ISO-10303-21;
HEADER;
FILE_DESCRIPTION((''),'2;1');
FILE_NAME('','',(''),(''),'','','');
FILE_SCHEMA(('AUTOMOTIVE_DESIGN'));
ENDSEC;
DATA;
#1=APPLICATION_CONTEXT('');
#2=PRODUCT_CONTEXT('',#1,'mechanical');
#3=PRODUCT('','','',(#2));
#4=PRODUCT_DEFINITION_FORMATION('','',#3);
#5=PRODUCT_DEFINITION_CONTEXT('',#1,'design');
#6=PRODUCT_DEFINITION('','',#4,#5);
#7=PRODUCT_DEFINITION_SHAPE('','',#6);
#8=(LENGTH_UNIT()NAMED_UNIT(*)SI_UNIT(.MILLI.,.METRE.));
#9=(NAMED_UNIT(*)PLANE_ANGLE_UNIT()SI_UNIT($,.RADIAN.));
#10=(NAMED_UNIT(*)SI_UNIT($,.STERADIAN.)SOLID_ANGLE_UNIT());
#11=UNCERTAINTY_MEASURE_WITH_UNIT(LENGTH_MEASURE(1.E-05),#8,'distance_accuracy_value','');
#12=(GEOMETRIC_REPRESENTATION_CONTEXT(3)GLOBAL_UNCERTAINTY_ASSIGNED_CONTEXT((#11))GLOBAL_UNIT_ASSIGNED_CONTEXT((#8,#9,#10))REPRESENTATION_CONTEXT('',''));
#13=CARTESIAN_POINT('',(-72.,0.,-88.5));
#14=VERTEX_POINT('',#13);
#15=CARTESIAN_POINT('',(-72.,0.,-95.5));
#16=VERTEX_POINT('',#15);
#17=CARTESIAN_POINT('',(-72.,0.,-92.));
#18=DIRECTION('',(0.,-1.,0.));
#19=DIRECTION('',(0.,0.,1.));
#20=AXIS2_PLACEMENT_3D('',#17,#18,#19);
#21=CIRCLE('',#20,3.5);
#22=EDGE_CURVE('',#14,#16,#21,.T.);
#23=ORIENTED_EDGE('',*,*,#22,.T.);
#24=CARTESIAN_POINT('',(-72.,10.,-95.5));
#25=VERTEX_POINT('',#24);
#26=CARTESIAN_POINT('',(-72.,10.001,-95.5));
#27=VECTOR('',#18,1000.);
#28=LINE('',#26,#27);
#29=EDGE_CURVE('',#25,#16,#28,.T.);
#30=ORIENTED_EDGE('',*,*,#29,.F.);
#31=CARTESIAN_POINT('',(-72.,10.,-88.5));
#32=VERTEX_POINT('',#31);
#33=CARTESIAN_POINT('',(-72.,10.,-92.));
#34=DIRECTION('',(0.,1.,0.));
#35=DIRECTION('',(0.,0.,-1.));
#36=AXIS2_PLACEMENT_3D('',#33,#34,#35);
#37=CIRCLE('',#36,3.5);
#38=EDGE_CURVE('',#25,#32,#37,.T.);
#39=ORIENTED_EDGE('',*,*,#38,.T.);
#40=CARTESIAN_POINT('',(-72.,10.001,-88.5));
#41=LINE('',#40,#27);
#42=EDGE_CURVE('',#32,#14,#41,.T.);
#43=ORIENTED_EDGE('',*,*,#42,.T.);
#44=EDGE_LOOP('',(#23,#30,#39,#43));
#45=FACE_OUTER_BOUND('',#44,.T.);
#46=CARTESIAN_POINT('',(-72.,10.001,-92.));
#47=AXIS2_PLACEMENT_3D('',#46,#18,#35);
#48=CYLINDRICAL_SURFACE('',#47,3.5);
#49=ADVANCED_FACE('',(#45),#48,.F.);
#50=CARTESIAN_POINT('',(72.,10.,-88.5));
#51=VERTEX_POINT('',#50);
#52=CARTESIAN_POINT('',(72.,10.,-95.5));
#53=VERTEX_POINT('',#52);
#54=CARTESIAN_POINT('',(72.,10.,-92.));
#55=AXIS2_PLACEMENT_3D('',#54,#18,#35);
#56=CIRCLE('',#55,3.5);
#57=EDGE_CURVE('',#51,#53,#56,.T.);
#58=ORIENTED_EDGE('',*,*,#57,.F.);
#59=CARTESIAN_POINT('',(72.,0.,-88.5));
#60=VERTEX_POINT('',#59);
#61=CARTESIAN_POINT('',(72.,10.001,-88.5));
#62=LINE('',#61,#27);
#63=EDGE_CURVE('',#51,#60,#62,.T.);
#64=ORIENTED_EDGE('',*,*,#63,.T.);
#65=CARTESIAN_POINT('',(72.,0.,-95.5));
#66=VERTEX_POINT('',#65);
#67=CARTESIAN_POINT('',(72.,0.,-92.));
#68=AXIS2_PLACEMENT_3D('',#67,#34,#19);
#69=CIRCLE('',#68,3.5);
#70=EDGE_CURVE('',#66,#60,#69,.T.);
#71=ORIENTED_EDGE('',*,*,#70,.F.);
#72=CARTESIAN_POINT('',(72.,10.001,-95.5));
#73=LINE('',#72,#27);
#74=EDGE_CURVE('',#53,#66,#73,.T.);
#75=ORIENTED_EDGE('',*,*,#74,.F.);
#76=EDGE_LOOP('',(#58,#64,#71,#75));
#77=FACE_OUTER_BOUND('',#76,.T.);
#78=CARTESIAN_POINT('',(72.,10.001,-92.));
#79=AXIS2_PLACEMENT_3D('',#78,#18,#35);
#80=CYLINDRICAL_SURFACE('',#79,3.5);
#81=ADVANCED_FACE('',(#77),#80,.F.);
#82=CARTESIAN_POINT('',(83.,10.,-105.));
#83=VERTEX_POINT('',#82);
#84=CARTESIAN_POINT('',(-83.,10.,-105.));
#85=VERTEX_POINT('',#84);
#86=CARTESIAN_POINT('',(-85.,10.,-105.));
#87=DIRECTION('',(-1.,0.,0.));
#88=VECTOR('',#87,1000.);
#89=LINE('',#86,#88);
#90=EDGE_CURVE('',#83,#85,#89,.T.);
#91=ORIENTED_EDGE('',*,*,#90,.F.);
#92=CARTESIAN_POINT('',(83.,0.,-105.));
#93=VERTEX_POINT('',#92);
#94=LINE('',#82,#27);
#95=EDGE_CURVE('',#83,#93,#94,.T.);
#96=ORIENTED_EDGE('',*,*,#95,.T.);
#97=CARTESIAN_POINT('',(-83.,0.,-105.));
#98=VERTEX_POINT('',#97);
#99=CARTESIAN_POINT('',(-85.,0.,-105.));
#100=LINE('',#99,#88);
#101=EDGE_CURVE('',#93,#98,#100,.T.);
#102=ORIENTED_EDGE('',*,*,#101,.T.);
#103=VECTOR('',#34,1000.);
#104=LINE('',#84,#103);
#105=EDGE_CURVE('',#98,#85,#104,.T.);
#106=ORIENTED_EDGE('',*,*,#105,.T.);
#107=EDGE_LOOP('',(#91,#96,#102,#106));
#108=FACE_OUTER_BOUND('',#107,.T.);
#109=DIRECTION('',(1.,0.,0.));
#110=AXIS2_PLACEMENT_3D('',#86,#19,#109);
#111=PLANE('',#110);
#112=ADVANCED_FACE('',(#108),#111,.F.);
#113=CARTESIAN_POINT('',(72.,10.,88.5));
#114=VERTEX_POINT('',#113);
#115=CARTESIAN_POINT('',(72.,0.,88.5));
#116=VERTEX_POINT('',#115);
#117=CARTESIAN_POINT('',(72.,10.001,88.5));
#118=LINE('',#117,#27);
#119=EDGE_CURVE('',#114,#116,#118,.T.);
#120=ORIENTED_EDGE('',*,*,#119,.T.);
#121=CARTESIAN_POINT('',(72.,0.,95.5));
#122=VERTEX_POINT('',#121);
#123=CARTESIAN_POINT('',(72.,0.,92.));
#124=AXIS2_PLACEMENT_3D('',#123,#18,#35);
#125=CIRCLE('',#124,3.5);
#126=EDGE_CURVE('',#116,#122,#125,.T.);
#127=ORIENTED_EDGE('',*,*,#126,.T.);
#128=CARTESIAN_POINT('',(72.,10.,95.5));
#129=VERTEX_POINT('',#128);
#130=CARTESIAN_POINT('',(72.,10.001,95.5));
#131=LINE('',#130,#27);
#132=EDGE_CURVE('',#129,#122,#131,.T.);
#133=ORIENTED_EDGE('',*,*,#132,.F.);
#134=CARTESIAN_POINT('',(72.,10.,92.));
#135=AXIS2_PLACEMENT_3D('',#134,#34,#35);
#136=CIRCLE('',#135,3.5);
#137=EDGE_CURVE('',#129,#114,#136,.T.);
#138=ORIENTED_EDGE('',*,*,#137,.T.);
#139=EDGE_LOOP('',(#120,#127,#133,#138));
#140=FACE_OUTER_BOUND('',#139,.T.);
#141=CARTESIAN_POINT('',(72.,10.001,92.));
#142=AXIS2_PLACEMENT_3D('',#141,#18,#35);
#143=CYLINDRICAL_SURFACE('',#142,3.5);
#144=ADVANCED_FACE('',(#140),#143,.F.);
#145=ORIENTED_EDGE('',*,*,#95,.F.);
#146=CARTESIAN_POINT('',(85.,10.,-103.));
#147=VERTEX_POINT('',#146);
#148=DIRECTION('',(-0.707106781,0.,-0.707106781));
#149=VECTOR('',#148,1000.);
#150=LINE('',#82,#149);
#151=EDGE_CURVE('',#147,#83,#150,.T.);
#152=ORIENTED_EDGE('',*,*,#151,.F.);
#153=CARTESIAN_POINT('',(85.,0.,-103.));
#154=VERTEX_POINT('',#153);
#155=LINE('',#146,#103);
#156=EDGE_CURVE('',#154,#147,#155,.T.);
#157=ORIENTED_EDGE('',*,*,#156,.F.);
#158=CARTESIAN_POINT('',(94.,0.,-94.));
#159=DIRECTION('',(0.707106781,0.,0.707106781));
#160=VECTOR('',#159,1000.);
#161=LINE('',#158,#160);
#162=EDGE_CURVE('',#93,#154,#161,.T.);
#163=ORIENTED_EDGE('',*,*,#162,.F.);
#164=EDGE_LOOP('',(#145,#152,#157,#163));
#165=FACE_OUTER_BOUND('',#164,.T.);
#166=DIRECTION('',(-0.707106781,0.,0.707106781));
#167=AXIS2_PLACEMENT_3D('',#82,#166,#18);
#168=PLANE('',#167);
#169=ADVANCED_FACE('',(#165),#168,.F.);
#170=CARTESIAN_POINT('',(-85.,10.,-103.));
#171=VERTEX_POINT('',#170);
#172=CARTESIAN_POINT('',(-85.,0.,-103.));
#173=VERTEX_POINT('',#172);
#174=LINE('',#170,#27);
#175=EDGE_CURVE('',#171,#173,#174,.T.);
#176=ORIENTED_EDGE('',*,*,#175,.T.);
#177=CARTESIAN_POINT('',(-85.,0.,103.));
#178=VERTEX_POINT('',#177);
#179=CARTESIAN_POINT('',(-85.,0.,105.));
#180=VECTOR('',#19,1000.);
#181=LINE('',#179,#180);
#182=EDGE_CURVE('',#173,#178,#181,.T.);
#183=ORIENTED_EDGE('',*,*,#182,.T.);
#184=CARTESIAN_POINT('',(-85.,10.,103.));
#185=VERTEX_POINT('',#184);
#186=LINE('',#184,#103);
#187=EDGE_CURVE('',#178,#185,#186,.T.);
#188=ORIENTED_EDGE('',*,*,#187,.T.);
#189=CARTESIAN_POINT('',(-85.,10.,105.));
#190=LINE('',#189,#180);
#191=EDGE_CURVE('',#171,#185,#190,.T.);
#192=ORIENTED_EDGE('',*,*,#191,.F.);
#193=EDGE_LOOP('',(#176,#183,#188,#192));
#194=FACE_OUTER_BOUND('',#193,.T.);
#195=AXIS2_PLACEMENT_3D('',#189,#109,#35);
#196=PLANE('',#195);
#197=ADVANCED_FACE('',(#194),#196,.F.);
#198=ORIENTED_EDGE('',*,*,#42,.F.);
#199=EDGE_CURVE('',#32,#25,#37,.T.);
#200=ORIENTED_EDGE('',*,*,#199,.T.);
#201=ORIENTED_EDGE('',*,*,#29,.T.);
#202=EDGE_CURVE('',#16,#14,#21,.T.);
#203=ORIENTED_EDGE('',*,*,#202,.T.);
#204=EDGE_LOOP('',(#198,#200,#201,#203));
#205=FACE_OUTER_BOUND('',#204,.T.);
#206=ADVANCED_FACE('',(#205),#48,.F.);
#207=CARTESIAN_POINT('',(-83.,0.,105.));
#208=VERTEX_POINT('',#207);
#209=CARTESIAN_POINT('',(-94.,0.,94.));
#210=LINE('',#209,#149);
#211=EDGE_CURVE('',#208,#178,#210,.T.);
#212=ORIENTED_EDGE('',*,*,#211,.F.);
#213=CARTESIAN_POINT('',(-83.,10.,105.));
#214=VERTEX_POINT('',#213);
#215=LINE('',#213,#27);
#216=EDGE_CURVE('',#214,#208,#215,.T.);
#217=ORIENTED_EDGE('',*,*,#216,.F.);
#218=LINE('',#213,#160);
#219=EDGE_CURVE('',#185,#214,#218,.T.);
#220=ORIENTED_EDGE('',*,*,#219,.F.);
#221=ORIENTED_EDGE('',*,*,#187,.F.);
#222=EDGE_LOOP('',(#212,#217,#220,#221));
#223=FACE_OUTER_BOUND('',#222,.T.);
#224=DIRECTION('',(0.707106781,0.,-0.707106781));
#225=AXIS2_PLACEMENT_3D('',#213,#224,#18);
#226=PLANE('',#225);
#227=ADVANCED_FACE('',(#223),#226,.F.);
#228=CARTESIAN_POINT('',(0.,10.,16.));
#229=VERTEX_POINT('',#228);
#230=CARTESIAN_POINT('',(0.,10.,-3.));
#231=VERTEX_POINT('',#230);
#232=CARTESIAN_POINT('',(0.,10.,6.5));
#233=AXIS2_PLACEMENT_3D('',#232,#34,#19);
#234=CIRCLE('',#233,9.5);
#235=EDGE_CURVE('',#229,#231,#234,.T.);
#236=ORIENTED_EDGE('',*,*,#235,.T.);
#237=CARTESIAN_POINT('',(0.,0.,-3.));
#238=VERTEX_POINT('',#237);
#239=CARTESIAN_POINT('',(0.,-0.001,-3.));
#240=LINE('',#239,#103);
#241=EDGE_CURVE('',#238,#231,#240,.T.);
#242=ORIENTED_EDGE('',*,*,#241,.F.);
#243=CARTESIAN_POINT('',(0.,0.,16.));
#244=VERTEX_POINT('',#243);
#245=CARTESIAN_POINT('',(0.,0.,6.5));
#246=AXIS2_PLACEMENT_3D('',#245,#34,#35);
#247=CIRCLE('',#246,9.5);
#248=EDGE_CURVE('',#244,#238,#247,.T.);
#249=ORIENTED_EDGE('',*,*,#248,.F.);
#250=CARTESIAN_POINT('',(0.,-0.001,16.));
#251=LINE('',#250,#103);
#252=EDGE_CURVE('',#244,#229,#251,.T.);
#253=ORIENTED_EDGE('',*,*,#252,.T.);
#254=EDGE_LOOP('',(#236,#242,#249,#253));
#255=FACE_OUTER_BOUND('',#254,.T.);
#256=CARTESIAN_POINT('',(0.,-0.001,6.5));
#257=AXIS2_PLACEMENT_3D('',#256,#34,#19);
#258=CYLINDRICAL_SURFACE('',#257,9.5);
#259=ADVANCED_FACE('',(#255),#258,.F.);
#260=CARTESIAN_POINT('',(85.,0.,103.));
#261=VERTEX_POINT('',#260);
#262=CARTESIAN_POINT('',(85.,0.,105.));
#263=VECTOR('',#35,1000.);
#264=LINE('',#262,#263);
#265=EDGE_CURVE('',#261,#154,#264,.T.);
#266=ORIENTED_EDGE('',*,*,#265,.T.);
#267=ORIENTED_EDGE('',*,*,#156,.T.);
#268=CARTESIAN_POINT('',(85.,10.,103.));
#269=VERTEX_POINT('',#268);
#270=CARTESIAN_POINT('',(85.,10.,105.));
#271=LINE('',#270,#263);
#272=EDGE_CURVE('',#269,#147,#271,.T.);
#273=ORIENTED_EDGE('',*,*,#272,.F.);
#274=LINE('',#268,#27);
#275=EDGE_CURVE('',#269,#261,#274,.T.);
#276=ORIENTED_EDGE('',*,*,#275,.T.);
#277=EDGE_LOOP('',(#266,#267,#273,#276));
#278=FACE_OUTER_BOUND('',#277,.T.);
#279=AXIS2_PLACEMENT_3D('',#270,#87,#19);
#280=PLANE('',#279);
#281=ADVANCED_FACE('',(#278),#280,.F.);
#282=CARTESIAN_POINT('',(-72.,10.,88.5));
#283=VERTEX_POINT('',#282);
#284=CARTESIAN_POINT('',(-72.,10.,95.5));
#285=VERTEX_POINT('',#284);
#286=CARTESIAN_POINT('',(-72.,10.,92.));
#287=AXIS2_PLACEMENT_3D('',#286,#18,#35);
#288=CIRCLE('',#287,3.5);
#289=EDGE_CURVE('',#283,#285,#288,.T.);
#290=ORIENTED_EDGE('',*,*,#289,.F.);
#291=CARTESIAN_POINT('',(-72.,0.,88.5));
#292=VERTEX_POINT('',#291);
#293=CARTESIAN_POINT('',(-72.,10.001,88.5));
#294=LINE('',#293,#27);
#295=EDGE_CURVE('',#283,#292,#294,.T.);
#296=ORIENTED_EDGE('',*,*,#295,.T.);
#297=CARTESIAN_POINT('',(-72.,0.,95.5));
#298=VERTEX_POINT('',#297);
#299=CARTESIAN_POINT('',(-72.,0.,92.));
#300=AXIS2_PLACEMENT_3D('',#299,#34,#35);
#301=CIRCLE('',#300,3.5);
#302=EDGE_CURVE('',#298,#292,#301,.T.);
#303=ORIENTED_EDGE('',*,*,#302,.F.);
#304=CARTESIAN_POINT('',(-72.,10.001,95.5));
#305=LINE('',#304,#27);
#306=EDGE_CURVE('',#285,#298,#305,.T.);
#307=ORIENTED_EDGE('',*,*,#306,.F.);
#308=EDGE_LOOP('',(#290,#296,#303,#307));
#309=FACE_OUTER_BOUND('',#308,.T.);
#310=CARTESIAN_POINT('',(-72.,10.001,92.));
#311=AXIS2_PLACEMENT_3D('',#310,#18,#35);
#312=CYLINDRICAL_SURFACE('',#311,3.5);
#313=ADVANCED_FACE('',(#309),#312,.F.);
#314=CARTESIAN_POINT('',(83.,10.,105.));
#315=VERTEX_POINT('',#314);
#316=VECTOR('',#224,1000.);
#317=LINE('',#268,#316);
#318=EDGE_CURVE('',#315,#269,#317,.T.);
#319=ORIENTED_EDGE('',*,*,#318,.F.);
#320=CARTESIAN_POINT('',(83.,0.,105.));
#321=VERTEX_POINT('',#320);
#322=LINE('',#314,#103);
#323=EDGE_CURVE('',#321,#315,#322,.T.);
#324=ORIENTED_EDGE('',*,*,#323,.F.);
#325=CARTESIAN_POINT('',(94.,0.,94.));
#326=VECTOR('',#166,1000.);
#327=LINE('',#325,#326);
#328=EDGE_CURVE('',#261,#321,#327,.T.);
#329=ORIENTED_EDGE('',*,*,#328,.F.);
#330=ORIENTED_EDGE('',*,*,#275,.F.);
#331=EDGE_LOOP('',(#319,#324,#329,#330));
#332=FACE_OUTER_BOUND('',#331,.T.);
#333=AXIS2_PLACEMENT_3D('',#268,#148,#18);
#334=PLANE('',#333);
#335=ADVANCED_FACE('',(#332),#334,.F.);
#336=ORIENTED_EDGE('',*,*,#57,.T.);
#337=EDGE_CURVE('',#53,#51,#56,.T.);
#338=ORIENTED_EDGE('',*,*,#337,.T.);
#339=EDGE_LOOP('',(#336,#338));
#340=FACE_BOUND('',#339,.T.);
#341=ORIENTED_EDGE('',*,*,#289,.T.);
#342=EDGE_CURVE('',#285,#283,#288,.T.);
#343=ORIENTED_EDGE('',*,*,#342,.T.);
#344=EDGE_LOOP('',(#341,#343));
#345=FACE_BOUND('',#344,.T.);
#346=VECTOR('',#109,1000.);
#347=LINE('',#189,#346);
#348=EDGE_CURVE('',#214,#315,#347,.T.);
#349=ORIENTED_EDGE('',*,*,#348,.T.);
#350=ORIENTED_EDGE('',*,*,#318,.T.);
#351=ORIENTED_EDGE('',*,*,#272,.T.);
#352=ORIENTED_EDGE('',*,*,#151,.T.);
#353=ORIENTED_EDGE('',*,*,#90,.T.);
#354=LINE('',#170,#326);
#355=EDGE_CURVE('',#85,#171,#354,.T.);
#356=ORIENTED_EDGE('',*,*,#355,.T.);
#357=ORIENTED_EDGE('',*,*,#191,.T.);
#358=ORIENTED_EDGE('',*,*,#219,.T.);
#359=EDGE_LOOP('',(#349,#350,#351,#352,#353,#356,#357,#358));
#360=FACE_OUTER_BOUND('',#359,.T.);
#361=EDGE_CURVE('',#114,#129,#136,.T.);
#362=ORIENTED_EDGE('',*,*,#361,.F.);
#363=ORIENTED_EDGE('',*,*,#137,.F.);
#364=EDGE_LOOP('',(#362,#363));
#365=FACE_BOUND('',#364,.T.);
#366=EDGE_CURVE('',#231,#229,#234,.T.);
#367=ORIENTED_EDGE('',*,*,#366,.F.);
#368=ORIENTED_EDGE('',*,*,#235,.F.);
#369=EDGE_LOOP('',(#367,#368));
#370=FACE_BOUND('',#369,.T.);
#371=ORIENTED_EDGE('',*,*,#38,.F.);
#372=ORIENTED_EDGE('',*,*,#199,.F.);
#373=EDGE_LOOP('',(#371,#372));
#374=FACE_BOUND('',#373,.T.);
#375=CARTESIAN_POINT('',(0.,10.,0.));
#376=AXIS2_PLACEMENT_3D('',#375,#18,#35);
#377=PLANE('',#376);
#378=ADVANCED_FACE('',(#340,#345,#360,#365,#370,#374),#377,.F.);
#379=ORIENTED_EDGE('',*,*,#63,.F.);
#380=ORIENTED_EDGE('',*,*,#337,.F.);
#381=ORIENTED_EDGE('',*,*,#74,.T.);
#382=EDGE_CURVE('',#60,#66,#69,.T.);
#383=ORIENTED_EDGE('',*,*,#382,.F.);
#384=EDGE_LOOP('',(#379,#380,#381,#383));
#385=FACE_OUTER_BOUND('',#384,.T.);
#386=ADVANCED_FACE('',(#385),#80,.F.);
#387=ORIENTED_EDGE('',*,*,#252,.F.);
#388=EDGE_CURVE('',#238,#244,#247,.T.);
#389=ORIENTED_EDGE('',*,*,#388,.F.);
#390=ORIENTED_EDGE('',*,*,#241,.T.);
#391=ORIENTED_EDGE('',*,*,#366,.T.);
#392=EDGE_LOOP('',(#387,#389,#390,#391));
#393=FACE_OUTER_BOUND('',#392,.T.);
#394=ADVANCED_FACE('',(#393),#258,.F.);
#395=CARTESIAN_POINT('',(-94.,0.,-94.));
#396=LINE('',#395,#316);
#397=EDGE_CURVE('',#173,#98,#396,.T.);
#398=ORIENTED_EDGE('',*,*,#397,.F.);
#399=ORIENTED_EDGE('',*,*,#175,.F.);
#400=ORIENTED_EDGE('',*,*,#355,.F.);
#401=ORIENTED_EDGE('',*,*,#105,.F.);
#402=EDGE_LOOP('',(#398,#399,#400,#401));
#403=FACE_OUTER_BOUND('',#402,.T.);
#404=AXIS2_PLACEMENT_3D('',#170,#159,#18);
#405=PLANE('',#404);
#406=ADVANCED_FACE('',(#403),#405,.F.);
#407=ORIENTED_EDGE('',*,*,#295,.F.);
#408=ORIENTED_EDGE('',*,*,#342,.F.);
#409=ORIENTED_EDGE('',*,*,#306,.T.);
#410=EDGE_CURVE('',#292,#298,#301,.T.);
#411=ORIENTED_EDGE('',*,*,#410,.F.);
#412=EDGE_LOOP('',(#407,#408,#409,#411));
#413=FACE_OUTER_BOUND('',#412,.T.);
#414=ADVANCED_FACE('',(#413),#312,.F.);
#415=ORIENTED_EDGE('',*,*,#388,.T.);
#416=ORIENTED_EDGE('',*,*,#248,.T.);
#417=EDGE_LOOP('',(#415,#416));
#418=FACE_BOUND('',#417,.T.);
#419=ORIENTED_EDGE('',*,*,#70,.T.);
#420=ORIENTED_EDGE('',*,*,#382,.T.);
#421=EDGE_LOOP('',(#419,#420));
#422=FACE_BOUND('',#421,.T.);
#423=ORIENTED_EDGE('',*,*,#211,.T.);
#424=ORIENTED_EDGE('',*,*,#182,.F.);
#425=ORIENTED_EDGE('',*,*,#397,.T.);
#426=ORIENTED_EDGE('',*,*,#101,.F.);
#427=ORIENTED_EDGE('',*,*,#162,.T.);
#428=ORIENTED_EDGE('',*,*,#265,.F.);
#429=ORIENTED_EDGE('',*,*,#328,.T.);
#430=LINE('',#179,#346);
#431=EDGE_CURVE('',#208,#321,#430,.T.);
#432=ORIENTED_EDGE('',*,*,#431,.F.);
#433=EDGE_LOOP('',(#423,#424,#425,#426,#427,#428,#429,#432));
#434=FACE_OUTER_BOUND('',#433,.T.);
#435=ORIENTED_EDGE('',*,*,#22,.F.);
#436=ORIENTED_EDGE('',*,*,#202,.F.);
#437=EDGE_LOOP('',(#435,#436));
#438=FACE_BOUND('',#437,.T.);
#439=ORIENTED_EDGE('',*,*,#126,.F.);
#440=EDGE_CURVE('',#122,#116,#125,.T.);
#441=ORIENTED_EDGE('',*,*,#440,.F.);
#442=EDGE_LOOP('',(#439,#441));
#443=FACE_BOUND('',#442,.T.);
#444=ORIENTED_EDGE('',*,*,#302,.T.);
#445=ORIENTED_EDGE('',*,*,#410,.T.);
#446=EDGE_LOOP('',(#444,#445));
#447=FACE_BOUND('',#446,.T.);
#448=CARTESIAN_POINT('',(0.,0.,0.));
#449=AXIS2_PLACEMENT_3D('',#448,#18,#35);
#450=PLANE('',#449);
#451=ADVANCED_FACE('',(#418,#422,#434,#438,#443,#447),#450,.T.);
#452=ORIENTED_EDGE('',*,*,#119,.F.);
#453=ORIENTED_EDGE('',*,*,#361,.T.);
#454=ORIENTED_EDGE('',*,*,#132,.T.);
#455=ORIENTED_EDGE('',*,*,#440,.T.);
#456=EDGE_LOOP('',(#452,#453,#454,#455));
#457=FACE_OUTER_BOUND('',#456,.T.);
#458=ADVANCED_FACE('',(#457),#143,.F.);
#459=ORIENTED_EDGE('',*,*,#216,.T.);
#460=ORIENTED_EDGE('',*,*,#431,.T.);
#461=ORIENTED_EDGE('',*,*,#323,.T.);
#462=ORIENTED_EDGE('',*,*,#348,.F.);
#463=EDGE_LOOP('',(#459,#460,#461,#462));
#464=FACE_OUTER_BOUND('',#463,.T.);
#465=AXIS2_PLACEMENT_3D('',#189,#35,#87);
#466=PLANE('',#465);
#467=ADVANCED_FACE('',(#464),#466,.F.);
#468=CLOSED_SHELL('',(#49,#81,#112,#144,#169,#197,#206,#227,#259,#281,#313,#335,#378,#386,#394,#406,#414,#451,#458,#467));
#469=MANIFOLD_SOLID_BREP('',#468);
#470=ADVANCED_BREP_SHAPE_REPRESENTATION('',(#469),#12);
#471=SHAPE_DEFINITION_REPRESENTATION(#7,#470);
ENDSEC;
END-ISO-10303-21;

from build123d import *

# Parameters (mm, degrees)
SKETCH_1_W               = 170
SKETCH_1_H               = 210
EXTRUDE_1_DEPTH          = 10
CUT_EXTRUDE_1_REACH      = 137.462
SKETCH_2_R               = 9.5
CUT_EXTRUDE_2_REACH      = 137.462
SKETCH_3_R               = 3.5
MIRROR_2_COPY_1_REACH    = 137.462
MIRROR_2_COPY_1_SKETCH_R = 3.5
CHAMFER_1_SIZE           = 2


with BuildPart() as part:
    # 草图1 → 凸台-拉伸1 (new body)
    with BuildSketch(Plane(origin=(0, 0, 0), x_dir=(1, 0, 0), z_dir=(0, 1, 0))):
        Rectangle(SKETCH_1_W, SKETCH_1_H)
    extrude(amount=EXTRUDE_1_DEPTH)

    # 草图2 → 切除-拉伸1 (cut, up to next)
    with BuildSketch(Plane(origin=(0, 10, 0), x_dir=(1, 0, 0), z_dir=(0, 1, 0)), mode=Mode.PRIVATE) as cut_extrude_1_sk1:
        with Locations(Location((0, -6.5, 0), (0, 0, 270))):
            Circle(SKETCH_2_R)
    cut_extrude_1_tool1 = extrude(cut_extrude_1_sk1.sketch, amount=-CUT_EXTRUDE_1_REACH, mode=Mode.PRIVATE) & part.part
    add(cut_extrude_1_tool1.solids().sort_by_distance((0, 10, 6.5))[0], mode=Mode.SUBTRACT)

    # 草图3 → 切除-拉伸2 (cut, up to next)
    with BuildSketch(Plane.XZ, mode=Mode.PRIVATE) as cut_extrude_2_sk1:
        with Locations(Location((72, 92, 0), (0, 0, 270))):
            Circle(SKETCH_3_R)
    cut_extrude_2_tool1 = extrude(cut_extrude_2_sk1.sketch, amount=-CUT_EXTRUDE_2_REACH, mode=Mode.PRIVATE) & part.part
    cut_extrude_2 = cut_extrude_2_tool1.solids().sort_by_distance((72, 0, 92))[0]
    add(cut_extrude_2, mode=Mode.SUBTRACT)

    # 镜向1: 切除-拉伸2 across plane
    add(cut_extrude_2.mirror(Plane(origin=(0, 0, 0), x_dir=(0, 0, 1), z_dir=(1, 0, 0))), mode=Mode.SUBTRACT)

    # 镜向2: 切除-拉伸2 across plane
    add(cut_extrude_2.mirror(Plane.XY), mode=Mode.SUBTRACT)

    # 镜向2 copy 1 sketch → 镜向2 copy 1 (cut, up to next)
    with BuildSketch(Plane(origin=(0, 0, 0), x_dir=(-1, 0, 0), z_dir=(0, -1, 0)), mode=Mode.PRIVATE) as mirror_2_copy_1_sk1:
        with Locations(Location((72, 92, 0), (0, 0, 270))):
            Circle(MIRROR_2_COPY_1_SKETCH_R)
    mirror_2_copy_1_tool1 = extrude(mirror_2_copy_1_sk1.sketch, amount=-MIRROR_2_COPY_1_REACH, mode=Mode.PRIVATE) & part.part
    add(mirror_2_copy_1_tool1.solids().sort_by_distance((-72, 0, -92))[0], mode=Mode.SUBTRACT)

    # 倒角1
    chamfer_1_edges = [part.edges().sort_by_distance(p)[0] for p in [
        (85, 5, 105),
        (-85, 5, 105),
        (-85, 5, -105),
        (85, 5, -105),
    ]]
    chamfer(chamfer_1_edges, length=CHAMFER_1_SIZE)


solid = part.part
